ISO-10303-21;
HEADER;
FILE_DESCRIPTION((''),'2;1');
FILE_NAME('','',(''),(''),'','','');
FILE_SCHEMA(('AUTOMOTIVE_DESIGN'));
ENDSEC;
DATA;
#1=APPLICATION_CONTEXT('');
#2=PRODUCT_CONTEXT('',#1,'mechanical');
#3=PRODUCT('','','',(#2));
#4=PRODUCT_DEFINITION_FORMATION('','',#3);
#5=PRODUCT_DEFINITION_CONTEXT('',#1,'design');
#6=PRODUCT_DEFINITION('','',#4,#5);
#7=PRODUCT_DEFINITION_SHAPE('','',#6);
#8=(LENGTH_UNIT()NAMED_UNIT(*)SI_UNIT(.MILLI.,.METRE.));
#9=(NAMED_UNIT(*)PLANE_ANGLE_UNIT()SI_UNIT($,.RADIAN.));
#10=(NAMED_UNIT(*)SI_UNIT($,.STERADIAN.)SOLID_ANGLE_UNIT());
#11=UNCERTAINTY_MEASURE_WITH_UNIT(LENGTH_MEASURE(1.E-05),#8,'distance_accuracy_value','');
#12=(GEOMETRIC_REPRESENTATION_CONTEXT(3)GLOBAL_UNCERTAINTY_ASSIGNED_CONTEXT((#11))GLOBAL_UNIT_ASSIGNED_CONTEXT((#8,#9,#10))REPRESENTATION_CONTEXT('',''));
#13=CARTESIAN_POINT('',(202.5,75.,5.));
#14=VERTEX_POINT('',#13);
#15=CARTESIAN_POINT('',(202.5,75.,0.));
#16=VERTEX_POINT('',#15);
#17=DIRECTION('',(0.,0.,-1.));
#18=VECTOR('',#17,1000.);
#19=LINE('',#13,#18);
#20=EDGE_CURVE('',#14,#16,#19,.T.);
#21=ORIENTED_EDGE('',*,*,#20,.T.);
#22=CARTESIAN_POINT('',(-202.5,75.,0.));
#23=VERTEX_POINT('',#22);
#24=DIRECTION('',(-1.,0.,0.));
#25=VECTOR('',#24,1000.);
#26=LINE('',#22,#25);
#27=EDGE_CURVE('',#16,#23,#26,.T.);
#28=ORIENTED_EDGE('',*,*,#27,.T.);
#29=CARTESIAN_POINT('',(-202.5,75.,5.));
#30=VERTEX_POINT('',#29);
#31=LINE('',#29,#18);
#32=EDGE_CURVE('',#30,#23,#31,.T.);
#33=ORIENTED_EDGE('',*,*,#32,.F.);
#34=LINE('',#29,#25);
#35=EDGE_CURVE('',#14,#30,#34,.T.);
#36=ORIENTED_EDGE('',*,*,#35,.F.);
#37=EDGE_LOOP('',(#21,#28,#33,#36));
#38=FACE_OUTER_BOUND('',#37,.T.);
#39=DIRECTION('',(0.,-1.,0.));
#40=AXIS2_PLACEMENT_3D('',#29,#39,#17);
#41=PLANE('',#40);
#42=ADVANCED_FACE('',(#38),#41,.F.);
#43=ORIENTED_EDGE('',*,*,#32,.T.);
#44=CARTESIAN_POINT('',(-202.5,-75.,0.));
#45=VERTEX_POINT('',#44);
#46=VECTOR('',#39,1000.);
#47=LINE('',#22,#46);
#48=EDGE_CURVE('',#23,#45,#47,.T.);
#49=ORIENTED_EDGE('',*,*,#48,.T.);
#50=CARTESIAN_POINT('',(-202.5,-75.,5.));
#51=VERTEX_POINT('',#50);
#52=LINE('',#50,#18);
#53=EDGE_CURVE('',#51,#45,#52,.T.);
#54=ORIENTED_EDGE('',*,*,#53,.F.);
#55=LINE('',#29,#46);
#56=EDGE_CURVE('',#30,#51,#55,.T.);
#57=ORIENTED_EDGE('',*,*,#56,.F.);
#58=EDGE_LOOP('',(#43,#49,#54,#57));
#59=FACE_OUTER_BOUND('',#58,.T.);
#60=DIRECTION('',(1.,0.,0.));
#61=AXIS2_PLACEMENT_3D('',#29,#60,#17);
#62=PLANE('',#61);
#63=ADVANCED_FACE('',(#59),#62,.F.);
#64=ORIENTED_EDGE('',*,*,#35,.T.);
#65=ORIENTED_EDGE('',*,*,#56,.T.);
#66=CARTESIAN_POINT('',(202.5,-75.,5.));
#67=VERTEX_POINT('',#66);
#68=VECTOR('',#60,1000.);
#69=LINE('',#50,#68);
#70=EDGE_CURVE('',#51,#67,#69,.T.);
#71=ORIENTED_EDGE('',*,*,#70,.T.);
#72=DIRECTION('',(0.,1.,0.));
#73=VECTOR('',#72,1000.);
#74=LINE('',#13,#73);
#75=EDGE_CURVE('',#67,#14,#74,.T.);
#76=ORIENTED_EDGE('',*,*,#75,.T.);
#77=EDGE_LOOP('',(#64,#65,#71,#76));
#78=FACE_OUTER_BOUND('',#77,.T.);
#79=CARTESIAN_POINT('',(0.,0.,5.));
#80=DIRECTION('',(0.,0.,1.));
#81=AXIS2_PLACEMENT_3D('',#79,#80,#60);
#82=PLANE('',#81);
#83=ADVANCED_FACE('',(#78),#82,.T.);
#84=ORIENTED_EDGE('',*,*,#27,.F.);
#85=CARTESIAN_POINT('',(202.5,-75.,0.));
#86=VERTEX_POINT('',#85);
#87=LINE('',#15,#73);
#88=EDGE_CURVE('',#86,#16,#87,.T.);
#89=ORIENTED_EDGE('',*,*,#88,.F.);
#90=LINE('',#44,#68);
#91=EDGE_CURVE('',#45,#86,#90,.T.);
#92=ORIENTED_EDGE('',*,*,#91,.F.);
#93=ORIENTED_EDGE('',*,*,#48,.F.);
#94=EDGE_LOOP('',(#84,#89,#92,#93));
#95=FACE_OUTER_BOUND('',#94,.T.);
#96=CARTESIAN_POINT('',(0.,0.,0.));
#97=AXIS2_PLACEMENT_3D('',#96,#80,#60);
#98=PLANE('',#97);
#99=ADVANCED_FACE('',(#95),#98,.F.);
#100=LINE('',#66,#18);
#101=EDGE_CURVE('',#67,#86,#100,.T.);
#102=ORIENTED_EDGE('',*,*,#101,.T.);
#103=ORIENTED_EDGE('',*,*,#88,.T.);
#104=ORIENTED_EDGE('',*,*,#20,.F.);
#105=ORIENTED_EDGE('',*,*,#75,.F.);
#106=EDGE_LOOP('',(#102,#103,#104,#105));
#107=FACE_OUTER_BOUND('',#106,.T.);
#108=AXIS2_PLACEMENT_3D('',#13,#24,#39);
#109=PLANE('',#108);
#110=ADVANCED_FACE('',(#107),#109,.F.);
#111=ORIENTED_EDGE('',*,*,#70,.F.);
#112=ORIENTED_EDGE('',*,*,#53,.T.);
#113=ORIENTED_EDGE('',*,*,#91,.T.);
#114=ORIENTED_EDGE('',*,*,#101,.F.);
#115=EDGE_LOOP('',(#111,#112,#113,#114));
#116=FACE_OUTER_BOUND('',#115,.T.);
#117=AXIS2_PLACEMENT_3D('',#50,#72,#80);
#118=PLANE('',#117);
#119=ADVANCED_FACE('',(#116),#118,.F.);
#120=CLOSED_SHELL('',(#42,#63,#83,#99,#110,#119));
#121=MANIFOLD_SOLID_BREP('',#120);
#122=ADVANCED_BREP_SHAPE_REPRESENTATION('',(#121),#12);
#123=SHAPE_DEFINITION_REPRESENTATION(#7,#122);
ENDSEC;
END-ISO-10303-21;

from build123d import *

# Parameters (mm, degrees)
SKETCH_1_W      = 405
SKETCH_1_H      = 150
EXTRUDE_1_DEPTH = 5


with BuildPart() as part:
    # 草图1 → 凸台-拉伸1 (new body)
    with BuildSketch(Plane.XY):
        Rectangle(SKETCH_1_W, SKETCH_1_H)
    extrude(amount=EXTRUDE_1_DEPTH)


solid = part.part
